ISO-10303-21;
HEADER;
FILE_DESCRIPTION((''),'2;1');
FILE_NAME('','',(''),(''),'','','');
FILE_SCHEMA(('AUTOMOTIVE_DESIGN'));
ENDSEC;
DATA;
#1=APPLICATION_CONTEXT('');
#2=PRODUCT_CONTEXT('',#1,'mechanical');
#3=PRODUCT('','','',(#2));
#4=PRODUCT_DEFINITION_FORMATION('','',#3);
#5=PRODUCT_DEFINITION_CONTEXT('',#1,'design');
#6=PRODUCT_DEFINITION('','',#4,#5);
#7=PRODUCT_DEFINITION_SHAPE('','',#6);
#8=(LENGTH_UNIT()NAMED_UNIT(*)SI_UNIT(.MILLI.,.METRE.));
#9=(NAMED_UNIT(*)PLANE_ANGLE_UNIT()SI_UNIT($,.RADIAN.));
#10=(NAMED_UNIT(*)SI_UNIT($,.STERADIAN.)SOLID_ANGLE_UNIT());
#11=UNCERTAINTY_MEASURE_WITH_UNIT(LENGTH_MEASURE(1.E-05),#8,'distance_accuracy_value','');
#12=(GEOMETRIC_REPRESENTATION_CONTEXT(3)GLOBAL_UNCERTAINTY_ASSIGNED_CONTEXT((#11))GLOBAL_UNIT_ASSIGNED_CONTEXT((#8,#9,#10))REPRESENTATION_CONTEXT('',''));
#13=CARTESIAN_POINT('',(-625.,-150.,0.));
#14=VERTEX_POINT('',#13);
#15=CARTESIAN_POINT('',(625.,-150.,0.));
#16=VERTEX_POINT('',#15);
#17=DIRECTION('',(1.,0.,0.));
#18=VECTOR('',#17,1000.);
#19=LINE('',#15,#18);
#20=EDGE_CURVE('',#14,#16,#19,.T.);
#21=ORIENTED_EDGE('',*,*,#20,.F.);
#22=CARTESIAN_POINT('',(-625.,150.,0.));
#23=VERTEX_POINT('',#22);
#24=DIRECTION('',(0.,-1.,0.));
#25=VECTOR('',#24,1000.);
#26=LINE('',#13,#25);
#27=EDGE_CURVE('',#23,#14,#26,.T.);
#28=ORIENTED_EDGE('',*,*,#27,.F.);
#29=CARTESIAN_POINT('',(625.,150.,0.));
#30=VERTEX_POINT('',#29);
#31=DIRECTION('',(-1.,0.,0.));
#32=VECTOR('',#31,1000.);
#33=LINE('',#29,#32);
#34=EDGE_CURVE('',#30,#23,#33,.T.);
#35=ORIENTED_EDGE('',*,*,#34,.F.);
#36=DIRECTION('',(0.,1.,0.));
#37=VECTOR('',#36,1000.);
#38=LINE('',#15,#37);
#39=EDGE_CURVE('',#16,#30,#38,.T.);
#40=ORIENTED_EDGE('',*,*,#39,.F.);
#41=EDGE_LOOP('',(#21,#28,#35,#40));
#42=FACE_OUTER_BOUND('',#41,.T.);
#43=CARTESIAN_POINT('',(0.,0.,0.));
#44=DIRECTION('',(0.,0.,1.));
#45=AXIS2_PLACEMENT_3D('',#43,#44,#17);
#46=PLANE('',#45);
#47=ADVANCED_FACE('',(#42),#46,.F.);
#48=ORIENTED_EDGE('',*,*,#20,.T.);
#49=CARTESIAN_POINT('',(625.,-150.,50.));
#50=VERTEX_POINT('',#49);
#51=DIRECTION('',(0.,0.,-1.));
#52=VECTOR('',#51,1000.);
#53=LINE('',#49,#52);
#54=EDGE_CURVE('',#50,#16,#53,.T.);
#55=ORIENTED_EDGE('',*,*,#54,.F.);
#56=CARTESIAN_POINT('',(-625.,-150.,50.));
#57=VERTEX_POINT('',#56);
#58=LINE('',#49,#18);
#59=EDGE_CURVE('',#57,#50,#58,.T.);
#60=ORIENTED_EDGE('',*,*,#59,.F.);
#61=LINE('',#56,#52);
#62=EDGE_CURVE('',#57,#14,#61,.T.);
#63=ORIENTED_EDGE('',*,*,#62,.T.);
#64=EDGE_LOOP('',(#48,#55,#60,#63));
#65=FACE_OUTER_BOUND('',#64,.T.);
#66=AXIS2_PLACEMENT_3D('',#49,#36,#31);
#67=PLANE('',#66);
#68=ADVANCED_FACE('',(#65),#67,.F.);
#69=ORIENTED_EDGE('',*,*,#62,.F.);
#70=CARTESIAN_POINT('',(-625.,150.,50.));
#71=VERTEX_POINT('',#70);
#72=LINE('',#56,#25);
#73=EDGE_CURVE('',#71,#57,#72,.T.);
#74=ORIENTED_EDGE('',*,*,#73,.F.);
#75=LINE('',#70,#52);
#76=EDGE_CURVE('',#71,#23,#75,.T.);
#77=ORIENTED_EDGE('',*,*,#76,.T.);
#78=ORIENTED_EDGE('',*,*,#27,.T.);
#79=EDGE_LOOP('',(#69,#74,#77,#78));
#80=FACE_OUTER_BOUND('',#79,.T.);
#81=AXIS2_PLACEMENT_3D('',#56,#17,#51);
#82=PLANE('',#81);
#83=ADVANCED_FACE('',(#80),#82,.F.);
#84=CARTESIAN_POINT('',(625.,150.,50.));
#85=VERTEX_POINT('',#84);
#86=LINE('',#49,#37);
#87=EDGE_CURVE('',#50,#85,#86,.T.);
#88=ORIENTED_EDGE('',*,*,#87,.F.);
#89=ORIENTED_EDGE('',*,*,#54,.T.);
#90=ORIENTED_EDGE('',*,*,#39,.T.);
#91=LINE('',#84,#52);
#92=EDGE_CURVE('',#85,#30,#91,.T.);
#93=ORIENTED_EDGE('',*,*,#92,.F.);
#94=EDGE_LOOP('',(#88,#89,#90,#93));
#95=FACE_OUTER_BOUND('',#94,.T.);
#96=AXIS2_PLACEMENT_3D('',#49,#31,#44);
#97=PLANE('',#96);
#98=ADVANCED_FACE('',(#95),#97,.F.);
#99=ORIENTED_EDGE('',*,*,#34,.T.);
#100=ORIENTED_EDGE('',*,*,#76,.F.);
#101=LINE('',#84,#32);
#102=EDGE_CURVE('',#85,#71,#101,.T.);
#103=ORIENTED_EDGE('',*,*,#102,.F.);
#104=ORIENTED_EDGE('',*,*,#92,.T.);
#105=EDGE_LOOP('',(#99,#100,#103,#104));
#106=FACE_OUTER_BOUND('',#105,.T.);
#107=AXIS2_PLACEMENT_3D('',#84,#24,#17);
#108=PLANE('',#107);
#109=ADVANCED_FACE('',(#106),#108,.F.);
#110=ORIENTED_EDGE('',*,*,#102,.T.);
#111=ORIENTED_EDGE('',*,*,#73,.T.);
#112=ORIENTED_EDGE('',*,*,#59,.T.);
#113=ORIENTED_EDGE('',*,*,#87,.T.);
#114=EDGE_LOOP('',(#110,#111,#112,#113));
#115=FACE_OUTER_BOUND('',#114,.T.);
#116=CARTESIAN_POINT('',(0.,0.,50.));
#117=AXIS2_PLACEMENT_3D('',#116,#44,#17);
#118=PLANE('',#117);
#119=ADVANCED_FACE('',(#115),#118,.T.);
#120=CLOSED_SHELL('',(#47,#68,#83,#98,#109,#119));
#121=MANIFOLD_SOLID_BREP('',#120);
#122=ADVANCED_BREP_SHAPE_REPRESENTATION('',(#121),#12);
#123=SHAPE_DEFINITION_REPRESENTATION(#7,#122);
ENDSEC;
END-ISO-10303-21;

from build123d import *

# Parameters (mm, degrees)
SKETCH_1_W      = 1250
SKETCH_1_H      = 300
EXTRUDE_1_DEPTH = 50


with BuildPart() as part:
    # 草图1 → 凸台-拉伸1 (new body)
    with BuildSketch(Plane.XY):
        Rectangle(SKETCH_1_W, SKETCH_1_H)
    extrude(amount=EXTRUDE_1_DEPTH)


solid = part.part
